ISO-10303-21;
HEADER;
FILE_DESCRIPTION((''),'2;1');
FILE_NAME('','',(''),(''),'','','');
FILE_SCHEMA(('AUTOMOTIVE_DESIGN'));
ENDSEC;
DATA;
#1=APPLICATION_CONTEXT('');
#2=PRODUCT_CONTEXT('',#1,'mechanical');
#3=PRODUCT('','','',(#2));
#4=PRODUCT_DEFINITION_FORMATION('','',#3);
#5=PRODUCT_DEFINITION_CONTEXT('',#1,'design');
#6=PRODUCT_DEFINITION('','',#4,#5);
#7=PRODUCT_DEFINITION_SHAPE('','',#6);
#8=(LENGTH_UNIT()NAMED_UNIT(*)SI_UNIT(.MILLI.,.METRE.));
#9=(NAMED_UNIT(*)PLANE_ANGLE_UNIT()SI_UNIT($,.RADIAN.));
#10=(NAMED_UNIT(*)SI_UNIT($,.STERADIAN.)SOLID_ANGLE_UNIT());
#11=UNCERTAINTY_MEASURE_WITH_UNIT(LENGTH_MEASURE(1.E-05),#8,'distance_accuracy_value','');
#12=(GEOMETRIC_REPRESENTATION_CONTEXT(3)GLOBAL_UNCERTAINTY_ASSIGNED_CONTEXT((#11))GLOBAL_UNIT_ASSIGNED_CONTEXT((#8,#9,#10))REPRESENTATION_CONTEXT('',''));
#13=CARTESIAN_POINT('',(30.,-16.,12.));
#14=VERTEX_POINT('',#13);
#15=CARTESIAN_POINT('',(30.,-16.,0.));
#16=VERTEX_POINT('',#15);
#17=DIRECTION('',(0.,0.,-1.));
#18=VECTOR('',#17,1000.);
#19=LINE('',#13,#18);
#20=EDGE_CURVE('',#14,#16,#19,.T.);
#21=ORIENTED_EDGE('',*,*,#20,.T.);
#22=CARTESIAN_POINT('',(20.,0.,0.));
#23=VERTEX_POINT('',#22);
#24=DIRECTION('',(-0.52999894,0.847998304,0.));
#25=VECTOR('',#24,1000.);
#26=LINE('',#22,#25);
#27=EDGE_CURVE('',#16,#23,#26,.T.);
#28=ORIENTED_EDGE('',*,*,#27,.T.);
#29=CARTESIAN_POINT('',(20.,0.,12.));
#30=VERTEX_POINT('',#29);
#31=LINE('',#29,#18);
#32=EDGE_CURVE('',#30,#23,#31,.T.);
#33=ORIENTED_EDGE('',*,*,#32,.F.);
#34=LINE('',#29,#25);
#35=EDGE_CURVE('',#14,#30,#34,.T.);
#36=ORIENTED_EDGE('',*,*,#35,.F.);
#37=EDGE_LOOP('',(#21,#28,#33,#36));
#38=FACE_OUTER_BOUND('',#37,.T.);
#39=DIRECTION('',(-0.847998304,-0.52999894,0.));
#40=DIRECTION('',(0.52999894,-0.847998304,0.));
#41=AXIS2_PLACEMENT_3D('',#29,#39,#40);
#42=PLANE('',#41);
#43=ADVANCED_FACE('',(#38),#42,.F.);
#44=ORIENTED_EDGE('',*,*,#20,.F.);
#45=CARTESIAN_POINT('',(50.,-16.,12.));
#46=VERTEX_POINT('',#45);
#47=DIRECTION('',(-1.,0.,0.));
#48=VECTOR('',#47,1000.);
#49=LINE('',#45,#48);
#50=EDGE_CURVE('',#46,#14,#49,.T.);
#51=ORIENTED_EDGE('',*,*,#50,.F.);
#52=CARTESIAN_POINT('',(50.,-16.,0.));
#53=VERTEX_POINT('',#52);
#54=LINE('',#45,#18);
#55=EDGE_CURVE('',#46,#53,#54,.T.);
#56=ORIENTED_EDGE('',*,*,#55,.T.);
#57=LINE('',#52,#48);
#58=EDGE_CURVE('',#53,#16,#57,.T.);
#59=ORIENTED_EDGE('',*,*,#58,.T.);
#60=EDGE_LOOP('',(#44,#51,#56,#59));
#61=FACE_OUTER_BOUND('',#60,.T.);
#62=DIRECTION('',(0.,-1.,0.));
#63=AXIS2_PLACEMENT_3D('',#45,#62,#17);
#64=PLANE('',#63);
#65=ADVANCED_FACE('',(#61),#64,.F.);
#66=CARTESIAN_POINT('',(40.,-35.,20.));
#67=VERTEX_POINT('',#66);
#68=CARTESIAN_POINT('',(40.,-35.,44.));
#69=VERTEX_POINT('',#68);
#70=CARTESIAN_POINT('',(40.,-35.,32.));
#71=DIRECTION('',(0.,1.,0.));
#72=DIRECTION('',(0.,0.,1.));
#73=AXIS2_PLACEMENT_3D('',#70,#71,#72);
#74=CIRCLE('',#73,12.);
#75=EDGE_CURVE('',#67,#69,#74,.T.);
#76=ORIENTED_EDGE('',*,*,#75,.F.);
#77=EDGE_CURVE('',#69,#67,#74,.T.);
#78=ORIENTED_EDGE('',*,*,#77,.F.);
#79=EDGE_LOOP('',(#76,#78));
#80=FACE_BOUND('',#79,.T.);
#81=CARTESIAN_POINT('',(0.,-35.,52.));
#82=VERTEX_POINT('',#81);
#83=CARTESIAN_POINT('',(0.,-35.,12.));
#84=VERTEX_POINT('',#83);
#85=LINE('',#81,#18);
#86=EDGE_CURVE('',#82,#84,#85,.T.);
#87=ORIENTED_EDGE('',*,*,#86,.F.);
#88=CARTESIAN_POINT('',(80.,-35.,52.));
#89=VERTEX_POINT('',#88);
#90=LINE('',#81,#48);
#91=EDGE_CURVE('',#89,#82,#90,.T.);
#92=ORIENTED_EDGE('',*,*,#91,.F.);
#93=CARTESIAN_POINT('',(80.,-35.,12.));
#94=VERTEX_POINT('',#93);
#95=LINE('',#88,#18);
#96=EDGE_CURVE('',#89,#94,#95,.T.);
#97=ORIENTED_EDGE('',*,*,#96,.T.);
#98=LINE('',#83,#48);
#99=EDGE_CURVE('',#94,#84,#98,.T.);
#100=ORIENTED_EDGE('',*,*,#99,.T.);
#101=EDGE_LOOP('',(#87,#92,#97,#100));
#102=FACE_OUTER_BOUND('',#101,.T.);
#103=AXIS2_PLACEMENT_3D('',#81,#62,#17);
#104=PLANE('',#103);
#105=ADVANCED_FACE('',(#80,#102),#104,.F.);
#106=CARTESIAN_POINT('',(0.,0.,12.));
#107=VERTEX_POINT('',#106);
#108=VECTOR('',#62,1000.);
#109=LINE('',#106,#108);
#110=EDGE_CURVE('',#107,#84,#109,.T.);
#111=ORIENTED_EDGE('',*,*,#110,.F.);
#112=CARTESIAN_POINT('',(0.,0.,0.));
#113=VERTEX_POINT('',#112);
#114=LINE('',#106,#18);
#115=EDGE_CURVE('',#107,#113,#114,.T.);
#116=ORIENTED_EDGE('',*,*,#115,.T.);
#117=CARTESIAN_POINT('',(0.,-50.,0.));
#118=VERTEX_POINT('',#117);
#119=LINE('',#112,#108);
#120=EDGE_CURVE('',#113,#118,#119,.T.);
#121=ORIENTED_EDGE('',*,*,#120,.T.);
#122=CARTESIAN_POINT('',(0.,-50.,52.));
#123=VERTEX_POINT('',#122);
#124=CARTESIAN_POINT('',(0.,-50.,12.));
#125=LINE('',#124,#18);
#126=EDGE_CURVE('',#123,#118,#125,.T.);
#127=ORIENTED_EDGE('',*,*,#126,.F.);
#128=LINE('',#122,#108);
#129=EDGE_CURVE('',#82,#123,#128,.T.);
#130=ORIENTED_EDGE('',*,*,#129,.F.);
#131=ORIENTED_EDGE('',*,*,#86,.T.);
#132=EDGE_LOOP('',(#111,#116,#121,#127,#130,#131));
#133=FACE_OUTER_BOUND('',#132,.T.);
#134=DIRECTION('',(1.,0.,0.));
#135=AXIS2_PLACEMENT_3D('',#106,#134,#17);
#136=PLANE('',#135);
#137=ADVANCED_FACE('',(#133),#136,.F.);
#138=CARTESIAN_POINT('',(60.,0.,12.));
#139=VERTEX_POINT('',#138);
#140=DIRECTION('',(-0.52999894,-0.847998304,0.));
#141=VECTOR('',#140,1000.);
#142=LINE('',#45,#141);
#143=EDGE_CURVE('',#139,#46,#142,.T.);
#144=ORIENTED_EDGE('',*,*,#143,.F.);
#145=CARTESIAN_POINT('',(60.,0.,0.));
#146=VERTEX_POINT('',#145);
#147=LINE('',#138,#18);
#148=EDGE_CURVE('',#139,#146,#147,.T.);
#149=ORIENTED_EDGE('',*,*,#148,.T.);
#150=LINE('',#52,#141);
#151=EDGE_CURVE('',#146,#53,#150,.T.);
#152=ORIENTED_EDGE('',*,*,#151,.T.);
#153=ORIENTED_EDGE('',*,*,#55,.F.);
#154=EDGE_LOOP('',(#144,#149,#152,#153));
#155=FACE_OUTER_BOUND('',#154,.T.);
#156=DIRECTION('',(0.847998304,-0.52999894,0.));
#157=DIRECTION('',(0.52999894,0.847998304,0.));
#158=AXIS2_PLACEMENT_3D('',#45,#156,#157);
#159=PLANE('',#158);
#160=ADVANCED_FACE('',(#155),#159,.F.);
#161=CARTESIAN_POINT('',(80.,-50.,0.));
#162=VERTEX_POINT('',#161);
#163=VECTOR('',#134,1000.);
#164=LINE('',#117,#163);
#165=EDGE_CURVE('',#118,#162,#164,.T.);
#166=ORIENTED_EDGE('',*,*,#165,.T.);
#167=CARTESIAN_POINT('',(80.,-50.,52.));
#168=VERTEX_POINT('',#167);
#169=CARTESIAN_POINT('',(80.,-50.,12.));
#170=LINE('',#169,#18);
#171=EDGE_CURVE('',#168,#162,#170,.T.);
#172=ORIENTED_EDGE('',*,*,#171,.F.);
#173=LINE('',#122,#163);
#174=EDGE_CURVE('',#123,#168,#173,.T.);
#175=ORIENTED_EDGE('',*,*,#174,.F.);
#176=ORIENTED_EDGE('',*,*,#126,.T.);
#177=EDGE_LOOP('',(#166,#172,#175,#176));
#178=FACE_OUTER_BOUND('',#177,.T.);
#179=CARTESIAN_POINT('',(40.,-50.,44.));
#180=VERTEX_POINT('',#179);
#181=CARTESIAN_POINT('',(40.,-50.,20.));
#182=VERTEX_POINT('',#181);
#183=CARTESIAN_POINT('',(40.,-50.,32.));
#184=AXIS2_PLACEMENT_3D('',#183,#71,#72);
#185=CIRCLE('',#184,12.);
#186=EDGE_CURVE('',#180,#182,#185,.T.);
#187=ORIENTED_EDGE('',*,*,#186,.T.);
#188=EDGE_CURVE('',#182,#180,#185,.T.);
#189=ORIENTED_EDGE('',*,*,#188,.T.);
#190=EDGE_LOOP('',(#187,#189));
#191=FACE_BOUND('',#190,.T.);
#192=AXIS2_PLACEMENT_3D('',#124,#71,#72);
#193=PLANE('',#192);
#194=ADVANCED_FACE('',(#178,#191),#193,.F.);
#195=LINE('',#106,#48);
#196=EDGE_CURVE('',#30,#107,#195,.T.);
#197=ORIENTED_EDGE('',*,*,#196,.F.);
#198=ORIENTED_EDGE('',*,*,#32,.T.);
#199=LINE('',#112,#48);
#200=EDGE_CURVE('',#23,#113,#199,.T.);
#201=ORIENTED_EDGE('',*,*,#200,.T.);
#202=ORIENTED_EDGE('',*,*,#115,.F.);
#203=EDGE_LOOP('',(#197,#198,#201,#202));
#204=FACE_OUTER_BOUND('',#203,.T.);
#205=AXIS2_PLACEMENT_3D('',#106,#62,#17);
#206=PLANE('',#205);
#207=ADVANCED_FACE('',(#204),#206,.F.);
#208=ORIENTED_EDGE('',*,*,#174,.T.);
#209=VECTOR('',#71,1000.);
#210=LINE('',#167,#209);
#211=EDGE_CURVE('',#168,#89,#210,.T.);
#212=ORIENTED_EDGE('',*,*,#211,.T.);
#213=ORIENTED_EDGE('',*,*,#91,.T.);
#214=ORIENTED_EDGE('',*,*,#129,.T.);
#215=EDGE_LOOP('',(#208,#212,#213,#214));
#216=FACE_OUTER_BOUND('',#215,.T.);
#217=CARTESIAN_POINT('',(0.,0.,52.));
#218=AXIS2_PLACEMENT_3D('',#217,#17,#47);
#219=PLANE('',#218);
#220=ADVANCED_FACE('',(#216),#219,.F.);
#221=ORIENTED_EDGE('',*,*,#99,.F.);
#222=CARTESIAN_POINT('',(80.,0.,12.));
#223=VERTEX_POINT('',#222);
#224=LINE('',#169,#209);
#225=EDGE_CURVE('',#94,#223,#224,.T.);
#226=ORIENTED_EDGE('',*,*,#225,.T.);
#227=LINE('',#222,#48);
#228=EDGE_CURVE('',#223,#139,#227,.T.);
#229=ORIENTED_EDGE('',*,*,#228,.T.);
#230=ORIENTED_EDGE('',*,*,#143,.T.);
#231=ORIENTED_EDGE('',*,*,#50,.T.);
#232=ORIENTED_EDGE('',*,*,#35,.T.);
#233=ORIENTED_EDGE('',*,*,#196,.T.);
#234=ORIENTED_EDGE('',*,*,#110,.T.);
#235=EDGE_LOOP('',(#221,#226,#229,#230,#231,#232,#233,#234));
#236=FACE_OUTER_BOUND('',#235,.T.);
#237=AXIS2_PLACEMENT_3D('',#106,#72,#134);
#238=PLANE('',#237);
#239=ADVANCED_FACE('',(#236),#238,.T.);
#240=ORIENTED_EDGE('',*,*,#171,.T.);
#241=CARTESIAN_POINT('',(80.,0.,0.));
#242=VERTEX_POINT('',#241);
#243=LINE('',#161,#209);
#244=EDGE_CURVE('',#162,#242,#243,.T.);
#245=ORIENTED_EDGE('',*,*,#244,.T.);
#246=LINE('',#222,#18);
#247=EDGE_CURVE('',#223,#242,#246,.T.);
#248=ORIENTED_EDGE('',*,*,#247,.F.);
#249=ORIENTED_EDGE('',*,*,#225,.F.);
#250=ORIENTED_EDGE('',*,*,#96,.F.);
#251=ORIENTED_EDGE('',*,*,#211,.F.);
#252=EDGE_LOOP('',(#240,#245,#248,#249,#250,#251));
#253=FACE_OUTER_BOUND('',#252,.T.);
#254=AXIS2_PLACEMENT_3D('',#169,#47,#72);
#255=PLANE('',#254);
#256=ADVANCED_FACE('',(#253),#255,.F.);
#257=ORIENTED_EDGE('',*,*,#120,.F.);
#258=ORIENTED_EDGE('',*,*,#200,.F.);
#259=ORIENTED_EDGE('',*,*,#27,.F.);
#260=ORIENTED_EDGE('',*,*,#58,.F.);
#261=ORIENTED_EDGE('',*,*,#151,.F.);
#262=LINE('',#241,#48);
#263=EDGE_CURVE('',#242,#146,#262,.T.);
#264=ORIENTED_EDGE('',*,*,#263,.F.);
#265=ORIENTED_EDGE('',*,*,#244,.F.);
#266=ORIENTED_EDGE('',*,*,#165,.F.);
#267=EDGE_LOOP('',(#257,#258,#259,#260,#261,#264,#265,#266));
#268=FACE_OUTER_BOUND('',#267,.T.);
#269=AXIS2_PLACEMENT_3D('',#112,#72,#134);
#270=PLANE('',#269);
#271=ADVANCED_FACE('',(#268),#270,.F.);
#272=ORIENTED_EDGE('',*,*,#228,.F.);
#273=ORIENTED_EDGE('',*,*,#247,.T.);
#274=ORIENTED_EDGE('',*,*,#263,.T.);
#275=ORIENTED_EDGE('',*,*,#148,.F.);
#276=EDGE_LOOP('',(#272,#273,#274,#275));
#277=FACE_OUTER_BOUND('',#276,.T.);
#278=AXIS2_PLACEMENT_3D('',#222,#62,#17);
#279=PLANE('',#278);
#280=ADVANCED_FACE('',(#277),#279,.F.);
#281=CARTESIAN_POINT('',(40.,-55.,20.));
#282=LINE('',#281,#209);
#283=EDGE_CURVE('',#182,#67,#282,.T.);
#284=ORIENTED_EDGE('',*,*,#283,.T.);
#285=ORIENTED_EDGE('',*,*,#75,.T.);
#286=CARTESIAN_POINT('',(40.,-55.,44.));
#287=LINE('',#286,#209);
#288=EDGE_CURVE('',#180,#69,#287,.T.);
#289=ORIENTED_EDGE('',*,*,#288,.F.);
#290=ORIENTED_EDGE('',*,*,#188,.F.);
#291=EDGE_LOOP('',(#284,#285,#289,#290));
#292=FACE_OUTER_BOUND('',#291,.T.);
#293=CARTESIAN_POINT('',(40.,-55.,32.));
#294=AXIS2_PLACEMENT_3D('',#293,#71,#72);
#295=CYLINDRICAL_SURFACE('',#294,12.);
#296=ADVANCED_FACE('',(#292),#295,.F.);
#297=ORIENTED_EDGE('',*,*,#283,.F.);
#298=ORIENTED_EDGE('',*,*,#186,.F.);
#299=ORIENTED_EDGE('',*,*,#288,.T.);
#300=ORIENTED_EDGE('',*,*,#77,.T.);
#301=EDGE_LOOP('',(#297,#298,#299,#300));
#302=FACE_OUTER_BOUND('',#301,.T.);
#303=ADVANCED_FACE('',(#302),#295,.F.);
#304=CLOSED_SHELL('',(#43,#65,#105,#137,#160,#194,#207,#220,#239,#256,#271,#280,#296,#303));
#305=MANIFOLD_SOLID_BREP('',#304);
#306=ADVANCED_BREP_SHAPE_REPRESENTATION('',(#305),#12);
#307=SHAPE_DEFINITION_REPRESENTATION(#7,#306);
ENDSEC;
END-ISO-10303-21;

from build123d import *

# Parameters (mm, degrees)
UPRIGHT_V_NOTCH_PLATE_DEPTH = 12
BASE_PLATE_SKETCH_W         = 80
BASE_PLATE_SKETCH_H         = 15
BASE_PLATE_DEPTH            = 40
BASE_HOLE_SKETCH_24_R       = 12
BASE_HOLE_24_DEPTH          = 20


with BuildPart() as part:
    # Upright V-Notch Profile Sketch → Upright V-Notch Plate (new body)
    with BuildSketch(Plane.XY):
        Polygon((0, 0), (0, -50), (80, -50), (80, 0), (60, 0), (50, -16), (30, -16), (20, 0), align=None)
    extrude(amount=UPRIGHT_V_NOTCH_PLATE_DEPTH)

    # Base Plate Sketch → Base Plate (add)
    with BuildSketch(Plane.XY.offset(12)):
        with Locations((40, -42.5)):
            Rectangle(BASE_PLATE_SKETCH_W, BASE_PLATE_SKETCH_H)
    extrude(amount=BASE_PLATE_DEPTH)

    # Base Hole Sketch Ø24 → Base Hole Ø24 (cut)
    with BuildSketch(Plane(origin=(0, -35, 0), x_dir=(1, 0, 0), z_dir=(0, 1, 0))):
        with Locations(Location((40, -32, 0), (0, 0, 270))):
            Circle(BASE_HOLE_SKETCH_24_R)
    extrude(amount=-BASE_HOLE_24_DEPTH, mode=Mode.SUBTRACT)


solid = part.part
